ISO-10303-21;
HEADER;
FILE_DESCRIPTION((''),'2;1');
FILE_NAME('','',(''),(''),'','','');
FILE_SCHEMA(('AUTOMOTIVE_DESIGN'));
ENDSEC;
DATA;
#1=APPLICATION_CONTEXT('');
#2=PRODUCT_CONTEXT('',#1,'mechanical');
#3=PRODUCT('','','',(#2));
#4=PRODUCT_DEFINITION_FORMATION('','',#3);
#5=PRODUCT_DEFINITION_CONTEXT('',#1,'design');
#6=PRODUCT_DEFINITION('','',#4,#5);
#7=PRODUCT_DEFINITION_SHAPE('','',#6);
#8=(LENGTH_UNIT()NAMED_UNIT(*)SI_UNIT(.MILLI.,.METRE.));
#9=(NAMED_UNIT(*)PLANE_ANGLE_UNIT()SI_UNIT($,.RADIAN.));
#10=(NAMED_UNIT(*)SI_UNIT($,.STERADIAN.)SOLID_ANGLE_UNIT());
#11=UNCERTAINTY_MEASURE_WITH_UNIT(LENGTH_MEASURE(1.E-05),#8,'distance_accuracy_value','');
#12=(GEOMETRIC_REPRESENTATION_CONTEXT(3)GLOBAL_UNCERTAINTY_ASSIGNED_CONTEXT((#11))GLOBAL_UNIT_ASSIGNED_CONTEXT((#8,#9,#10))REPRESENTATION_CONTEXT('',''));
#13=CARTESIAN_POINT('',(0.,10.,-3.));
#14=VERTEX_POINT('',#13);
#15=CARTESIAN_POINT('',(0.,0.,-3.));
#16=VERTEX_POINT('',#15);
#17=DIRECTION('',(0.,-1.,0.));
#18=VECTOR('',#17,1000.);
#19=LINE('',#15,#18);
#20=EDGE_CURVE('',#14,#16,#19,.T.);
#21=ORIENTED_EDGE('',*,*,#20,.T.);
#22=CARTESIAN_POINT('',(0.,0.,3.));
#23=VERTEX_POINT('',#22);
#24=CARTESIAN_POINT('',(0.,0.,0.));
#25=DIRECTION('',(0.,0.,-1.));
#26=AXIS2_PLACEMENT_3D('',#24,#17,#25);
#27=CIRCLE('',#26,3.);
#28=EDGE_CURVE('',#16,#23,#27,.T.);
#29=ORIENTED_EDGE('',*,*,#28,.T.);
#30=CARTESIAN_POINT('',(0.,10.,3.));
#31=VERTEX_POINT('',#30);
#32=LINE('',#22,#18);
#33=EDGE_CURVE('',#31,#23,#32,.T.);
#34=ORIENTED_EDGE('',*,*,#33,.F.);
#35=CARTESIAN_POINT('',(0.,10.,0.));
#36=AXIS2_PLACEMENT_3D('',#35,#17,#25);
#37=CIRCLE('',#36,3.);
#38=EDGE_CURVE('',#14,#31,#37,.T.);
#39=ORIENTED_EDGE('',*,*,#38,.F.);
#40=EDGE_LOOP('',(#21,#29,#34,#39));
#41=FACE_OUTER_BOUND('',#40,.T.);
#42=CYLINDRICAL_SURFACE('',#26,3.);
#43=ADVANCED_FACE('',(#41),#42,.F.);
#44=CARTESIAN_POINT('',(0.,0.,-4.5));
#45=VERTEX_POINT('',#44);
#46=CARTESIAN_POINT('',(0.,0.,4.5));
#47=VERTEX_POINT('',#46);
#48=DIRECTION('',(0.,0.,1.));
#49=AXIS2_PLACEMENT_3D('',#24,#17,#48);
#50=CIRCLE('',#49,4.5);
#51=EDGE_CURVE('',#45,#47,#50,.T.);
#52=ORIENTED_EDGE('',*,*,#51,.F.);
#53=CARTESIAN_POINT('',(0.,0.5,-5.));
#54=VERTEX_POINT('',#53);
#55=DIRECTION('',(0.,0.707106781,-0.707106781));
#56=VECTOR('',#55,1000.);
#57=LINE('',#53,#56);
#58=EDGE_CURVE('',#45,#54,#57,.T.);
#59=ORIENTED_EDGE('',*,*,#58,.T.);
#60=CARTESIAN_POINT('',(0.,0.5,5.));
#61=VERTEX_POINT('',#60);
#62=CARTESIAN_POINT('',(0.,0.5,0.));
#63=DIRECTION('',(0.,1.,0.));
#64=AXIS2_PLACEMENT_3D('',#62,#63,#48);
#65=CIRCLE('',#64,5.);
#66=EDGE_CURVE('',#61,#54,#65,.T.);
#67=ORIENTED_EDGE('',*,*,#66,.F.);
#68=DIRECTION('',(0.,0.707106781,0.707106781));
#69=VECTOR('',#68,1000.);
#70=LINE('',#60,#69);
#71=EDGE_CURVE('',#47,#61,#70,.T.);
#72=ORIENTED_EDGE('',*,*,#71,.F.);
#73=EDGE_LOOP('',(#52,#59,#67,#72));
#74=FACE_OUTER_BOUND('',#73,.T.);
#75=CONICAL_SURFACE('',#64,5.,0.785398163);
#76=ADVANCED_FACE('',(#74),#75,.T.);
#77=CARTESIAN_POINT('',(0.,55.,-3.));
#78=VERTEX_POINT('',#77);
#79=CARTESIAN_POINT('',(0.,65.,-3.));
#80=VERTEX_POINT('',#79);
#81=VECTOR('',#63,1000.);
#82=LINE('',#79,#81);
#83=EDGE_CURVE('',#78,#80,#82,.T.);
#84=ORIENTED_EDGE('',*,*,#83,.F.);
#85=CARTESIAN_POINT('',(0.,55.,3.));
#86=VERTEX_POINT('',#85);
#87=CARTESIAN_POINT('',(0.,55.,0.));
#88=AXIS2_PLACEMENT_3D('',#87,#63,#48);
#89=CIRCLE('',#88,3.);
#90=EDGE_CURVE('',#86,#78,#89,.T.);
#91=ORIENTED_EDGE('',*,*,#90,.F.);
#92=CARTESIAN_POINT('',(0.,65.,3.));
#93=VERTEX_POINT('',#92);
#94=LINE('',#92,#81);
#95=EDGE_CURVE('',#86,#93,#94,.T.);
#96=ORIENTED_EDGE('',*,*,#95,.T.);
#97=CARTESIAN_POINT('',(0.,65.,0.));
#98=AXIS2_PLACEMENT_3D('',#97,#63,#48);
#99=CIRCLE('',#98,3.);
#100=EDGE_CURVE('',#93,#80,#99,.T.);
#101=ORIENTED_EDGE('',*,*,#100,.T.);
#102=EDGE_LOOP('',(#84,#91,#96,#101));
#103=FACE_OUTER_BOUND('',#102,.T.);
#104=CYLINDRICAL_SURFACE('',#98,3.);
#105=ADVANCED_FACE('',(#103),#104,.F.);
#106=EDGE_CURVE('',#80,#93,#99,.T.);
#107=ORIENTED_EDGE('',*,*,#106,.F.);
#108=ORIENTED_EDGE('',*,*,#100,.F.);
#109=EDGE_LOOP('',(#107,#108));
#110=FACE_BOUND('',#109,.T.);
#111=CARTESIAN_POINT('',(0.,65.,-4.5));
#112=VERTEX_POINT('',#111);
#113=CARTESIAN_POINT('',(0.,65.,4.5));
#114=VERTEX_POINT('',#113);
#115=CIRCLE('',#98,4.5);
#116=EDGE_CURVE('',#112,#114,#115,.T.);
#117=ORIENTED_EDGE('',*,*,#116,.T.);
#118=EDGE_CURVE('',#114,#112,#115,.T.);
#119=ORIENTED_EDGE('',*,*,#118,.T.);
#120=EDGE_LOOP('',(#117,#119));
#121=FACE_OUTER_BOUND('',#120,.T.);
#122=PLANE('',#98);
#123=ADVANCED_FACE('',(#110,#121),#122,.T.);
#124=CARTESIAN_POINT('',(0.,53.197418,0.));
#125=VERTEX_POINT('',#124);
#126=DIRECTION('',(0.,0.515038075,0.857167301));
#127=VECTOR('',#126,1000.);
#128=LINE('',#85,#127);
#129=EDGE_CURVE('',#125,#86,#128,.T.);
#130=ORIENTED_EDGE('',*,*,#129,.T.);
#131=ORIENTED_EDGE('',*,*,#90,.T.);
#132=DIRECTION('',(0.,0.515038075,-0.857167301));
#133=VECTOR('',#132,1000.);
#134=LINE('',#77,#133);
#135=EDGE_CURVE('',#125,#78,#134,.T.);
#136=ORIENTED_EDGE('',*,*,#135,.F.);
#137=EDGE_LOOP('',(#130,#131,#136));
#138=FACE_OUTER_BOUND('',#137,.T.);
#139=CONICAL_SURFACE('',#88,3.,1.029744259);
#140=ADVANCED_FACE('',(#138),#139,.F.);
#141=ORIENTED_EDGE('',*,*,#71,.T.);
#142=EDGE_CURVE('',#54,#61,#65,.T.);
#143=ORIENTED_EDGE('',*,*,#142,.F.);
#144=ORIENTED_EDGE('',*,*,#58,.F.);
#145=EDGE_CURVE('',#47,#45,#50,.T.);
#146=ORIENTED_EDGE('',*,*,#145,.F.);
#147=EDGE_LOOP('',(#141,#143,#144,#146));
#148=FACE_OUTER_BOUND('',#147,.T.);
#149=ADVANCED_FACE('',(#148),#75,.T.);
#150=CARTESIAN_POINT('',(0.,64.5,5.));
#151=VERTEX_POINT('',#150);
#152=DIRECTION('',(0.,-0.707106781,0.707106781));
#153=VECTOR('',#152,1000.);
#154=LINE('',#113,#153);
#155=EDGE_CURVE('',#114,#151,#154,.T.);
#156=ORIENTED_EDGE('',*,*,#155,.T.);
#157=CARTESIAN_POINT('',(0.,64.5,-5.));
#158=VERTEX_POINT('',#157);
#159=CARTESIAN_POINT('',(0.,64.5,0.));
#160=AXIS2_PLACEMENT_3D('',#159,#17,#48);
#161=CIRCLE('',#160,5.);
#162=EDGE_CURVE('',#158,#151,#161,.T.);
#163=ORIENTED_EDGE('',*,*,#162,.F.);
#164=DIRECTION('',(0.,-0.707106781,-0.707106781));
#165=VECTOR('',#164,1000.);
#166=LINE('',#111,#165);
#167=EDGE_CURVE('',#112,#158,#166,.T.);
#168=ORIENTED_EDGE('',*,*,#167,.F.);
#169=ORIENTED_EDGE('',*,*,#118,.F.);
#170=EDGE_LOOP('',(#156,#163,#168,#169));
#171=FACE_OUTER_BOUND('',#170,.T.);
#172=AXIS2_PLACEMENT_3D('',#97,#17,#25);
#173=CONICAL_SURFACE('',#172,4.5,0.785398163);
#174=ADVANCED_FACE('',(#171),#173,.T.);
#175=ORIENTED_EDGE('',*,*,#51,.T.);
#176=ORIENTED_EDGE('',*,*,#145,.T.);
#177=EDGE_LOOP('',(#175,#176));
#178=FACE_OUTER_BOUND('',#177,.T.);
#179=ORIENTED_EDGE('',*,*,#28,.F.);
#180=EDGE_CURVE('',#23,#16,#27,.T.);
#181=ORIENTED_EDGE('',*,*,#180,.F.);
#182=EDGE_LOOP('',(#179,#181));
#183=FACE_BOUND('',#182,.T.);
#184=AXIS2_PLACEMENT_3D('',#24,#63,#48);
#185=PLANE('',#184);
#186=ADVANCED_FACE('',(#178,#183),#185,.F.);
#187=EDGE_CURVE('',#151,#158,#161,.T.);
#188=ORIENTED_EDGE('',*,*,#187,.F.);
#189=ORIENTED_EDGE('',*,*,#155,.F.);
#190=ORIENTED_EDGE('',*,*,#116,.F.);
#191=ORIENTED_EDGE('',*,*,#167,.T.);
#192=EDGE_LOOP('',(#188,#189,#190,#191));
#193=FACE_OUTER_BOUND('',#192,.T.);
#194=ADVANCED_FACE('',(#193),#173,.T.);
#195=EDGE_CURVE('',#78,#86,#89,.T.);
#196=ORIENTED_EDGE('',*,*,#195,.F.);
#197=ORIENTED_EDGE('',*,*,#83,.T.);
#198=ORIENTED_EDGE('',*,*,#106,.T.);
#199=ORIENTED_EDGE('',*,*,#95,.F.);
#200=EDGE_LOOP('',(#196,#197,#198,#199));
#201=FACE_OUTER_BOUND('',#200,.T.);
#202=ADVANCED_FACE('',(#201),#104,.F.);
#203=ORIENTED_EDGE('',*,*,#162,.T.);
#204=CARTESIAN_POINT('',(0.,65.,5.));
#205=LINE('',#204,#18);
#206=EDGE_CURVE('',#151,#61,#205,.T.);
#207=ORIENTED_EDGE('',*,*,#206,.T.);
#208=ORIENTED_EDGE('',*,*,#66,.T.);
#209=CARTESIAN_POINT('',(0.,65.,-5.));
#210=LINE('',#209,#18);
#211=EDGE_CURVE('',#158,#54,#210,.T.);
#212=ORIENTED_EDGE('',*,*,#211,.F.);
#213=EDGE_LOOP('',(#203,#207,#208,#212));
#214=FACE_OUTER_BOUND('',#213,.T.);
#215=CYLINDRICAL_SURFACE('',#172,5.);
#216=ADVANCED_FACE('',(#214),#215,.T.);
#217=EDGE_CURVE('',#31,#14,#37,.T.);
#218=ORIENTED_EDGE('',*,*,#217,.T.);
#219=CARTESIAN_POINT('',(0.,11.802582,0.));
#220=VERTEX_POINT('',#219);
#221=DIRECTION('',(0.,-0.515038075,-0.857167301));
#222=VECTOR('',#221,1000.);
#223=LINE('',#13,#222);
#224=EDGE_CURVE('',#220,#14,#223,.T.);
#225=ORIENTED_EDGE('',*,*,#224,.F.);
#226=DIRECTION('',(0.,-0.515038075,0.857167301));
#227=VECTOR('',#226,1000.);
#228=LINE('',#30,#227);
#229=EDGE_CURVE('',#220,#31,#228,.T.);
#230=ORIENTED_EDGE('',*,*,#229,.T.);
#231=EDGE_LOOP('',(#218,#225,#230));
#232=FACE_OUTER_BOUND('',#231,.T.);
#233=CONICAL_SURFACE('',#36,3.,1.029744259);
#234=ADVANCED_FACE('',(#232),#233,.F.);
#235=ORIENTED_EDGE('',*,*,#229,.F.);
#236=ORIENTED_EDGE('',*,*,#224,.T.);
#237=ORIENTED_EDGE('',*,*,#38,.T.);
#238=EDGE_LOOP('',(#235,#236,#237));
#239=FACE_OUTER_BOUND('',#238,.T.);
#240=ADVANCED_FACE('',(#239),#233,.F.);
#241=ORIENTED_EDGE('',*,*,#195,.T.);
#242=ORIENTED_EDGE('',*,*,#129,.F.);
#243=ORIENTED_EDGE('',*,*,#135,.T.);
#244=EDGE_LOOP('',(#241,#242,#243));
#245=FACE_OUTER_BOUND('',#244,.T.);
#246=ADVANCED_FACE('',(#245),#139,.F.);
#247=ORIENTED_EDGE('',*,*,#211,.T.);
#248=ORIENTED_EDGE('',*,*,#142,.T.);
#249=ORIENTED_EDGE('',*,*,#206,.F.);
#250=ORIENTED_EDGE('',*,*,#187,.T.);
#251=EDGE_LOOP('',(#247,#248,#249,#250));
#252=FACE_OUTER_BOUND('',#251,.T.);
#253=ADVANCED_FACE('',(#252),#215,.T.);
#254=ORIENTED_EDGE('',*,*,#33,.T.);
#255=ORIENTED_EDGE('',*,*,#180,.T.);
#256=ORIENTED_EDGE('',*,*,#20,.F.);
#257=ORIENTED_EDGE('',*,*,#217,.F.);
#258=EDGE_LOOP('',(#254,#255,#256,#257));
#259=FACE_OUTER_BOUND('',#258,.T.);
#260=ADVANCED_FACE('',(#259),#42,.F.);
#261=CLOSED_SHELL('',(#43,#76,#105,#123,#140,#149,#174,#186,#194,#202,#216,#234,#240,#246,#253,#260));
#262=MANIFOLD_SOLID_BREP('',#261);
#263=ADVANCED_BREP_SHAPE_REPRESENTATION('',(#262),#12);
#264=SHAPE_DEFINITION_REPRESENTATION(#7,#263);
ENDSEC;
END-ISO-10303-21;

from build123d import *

# Parameters (mm, degrees)
SKETCH1_R           = 5
BOSS_EXTRUDE1_DEPTH = 65
CHAMFER1_SIZE       = 0.5


with BuildPart() as part:
    # Sketch1 → Boss-Extrude1 (new body)
    with BuildSketch(Plane(origin=(0, 0, 0), x_dir=(1, 0, 0), z_dir=(0, 1, 0))):
        with Locations(Location((0, 0, 0), (0, 0, 270))):
            Circle(SKETCH1_R)
    extrude(amount=BOSS_EXTRUDE1_DEPTH)

    # Sketch2 → Ø18.0 (18) Diameter Hole1 (revolve, cut)
    with BuildSketch(Plane(origin=(0, 65, 0), x_dir=(0, 0, 1), z_dir=(1, 0, 0))):
        Polygon((0, 0), (0, 11.802581857), (3, 10), (3, 0), align=None)
    f_18_0_18_diameter_hole1 = revolve(axis=Axis((0, 71.35, 0), (0, -1, 0)), mode=Mode.SUBTRACT)

    # Mirror1: Ø18.0 (18) Diameter Hole1 across plane
    add(f_18_0_18_diameter_hole1.mirror(Plane.ZX.offset(32.5)), mode=Mode.SUBTRACT)

    # Chamfer1
    chamfer1_edges = [part.edges().sort_by_distance(p)[0] for p in [
        (0, 0, -5),
        (0, 65, -5),
    ]]
    chamfer(chamfer1_edges, length=CHAMFER1_SIZE)


solid = part.part
